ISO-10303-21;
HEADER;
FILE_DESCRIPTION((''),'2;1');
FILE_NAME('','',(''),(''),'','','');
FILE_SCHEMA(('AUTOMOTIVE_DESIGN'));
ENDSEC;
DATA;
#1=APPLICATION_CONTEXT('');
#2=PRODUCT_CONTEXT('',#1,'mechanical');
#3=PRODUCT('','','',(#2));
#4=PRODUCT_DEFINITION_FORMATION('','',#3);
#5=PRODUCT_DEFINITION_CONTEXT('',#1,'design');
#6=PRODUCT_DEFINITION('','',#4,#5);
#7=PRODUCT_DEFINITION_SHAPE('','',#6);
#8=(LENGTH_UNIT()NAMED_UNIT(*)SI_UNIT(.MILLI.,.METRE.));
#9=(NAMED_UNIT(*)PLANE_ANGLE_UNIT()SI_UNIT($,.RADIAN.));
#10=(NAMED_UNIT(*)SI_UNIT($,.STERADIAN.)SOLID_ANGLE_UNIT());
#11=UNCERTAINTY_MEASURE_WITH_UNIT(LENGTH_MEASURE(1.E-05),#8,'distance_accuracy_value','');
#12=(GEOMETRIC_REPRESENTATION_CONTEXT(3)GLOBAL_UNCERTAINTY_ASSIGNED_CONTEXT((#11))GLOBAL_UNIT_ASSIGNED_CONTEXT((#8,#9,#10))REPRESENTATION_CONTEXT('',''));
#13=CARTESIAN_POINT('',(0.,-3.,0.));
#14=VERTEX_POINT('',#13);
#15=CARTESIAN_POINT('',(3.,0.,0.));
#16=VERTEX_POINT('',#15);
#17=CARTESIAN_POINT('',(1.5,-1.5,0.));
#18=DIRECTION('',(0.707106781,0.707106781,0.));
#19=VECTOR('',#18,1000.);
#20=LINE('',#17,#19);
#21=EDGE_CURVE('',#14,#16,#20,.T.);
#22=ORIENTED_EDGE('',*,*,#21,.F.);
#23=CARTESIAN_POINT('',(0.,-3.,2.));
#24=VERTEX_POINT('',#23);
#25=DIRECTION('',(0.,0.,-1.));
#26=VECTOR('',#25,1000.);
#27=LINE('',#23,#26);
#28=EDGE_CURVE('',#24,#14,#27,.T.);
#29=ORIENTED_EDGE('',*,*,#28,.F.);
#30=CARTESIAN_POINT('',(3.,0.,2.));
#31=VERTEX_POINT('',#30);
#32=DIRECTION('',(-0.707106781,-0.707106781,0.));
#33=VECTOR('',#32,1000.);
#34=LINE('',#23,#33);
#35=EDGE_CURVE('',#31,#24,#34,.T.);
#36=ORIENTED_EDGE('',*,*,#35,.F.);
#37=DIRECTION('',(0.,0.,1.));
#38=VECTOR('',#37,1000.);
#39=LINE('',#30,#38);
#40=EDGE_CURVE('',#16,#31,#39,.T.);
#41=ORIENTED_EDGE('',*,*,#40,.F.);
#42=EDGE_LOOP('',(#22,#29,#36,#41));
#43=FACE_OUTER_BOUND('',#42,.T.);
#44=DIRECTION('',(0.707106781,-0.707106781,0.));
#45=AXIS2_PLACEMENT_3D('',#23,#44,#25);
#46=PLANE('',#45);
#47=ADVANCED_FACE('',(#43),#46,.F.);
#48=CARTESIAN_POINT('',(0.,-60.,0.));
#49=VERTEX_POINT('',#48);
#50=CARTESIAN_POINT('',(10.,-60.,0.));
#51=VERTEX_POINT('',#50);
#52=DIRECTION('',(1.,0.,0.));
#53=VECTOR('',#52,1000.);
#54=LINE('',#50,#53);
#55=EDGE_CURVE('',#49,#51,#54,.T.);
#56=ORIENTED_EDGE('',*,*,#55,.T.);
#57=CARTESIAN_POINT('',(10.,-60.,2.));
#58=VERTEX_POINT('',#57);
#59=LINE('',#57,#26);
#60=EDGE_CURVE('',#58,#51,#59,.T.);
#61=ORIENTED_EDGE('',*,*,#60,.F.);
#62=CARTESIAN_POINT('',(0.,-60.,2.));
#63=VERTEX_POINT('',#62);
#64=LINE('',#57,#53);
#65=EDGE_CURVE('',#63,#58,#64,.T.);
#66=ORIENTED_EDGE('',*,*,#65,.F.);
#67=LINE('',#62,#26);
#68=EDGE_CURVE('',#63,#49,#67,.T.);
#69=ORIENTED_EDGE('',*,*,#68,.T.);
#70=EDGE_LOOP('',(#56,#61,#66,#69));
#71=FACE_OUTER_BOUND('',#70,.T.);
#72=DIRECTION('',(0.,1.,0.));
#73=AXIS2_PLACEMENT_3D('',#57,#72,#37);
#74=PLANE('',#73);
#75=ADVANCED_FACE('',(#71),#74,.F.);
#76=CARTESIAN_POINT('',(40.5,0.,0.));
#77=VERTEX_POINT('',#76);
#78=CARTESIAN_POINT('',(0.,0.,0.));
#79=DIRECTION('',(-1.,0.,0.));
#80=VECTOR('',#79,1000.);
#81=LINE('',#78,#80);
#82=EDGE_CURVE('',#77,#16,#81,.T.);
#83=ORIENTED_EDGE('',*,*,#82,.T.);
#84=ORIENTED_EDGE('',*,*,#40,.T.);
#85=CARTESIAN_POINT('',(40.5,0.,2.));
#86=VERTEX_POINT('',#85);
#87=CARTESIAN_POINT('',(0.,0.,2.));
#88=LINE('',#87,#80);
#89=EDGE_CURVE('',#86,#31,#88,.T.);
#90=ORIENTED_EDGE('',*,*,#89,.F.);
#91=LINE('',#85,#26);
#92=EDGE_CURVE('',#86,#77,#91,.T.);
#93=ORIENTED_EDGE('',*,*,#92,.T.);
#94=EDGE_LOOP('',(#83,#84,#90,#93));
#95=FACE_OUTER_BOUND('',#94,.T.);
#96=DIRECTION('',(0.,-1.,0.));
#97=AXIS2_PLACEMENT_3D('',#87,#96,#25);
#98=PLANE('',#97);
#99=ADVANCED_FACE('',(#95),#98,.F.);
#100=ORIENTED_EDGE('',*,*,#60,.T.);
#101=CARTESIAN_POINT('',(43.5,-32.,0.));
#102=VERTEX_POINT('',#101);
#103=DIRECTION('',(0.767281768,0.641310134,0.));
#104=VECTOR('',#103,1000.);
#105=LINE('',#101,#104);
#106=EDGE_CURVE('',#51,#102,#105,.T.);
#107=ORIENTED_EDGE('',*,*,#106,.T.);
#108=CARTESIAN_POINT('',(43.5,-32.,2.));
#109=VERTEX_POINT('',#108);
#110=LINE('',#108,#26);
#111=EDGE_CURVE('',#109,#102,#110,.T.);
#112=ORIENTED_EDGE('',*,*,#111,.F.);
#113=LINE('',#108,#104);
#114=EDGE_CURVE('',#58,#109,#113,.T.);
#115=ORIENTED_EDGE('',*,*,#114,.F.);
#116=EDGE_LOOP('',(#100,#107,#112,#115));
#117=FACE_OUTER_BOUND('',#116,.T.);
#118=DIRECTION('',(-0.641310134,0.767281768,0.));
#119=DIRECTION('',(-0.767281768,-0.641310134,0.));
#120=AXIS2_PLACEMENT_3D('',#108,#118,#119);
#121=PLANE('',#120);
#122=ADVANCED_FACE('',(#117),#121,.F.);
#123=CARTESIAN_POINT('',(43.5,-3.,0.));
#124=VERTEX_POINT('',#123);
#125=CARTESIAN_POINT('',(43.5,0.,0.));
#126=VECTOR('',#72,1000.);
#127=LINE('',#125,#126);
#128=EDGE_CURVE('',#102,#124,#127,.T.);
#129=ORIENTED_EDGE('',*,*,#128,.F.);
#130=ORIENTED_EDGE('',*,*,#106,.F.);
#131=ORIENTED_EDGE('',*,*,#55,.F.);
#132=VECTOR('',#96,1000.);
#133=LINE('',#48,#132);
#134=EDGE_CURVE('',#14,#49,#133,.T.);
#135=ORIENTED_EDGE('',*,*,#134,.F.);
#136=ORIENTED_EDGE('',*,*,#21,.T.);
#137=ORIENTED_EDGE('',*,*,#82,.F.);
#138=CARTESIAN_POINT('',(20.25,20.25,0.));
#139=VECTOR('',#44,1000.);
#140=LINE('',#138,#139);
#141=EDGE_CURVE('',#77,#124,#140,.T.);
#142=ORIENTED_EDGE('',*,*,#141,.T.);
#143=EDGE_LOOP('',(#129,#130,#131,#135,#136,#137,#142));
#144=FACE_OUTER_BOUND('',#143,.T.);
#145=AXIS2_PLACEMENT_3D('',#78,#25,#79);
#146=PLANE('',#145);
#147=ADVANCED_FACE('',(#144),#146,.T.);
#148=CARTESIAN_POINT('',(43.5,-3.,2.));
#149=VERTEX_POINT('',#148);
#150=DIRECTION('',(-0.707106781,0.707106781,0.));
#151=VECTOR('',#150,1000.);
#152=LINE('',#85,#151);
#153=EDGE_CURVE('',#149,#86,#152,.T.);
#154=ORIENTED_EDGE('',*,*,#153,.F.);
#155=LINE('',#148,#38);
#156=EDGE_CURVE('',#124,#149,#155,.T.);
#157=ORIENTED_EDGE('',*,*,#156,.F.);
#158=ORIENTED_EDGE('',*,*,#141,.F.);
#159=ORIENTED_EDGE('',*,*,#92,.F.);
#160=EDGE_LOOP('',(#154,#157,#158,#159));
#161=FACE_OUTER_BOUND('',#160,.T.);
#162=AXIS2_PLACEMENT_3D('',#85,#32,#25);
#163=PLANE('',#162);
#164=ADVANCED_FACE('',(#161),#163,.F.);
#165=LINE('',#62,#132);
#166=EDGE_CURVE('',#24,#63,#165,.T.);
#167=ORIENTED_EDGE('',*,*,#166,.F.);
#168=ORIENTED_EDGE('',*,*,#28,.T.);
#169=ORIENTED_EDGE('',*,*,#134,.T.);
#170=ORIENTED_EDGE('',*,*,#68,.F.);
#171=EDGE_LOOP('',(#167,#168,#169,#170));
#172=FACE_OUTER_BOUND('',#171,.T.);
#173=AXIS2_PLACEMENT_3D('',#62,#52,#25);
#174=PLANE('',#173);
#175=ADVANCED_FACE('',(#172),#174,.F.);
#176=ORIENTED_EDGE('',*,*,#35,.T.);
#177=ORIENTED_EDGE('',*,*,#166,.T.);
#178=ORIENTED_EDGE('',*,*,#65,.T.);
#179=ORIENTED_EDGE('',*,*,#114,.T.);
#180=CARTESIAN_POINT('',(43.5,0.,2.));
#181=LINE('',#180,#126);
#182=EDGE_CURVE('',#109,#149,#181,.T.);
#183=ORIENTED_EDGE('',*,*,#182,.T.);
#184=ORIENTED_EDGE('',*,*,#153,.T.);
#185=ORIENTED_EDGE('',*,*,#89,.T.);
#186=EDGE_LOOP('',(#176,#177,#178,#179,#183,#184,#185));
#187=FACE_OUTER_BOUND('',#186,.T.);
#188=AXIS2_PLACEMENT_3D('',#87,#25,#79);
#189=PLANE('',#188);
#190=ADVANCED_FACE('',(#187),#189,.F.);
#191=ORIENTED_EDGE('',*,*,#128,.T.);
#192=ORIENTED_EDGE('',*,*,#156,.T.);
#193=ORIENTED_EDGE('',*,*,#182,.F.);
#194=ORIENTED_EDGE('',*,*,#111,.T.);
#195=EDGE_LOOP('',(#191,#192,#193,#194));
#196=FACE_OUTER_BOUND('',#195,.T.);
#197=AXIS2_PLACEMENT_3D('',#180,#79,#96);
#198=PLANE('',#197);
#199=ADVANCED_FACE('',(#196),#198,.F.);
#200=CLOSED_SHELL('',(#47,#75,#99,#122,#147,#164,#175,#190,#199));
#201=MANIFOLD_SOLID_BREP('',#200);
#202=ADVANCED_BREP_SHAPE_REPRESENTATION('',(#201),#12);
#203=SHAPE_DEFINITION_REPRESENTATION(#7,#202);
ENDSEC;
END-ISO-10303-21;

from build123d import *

# Parameters (mm, degrees)
EXTRUDE_1_DEPTH = 2
CHAMFER_1_SIZE  = 3


with BuildPart() as part:
    # 草图1 → 凸台-拉伸1 (new body)
    with BuildSketch(Plane.XY):
        Polygon((0, 0), (43.5, 0), (43.5, -32), (10, -60), (0, -60), align=None)
    extrude(amount=EXTRUDE_1_DEPTH)

    # 倒角1
    chamfer_1_edges = [part.edges().sort_by_distance(p)[0] for p in [
        (0, 0, 1),
        (43.5, 0, 1),
    ]]
    chamfer(chamfer_1_edges, length=CHAMFER_1_SIZE)


solid = part.part
